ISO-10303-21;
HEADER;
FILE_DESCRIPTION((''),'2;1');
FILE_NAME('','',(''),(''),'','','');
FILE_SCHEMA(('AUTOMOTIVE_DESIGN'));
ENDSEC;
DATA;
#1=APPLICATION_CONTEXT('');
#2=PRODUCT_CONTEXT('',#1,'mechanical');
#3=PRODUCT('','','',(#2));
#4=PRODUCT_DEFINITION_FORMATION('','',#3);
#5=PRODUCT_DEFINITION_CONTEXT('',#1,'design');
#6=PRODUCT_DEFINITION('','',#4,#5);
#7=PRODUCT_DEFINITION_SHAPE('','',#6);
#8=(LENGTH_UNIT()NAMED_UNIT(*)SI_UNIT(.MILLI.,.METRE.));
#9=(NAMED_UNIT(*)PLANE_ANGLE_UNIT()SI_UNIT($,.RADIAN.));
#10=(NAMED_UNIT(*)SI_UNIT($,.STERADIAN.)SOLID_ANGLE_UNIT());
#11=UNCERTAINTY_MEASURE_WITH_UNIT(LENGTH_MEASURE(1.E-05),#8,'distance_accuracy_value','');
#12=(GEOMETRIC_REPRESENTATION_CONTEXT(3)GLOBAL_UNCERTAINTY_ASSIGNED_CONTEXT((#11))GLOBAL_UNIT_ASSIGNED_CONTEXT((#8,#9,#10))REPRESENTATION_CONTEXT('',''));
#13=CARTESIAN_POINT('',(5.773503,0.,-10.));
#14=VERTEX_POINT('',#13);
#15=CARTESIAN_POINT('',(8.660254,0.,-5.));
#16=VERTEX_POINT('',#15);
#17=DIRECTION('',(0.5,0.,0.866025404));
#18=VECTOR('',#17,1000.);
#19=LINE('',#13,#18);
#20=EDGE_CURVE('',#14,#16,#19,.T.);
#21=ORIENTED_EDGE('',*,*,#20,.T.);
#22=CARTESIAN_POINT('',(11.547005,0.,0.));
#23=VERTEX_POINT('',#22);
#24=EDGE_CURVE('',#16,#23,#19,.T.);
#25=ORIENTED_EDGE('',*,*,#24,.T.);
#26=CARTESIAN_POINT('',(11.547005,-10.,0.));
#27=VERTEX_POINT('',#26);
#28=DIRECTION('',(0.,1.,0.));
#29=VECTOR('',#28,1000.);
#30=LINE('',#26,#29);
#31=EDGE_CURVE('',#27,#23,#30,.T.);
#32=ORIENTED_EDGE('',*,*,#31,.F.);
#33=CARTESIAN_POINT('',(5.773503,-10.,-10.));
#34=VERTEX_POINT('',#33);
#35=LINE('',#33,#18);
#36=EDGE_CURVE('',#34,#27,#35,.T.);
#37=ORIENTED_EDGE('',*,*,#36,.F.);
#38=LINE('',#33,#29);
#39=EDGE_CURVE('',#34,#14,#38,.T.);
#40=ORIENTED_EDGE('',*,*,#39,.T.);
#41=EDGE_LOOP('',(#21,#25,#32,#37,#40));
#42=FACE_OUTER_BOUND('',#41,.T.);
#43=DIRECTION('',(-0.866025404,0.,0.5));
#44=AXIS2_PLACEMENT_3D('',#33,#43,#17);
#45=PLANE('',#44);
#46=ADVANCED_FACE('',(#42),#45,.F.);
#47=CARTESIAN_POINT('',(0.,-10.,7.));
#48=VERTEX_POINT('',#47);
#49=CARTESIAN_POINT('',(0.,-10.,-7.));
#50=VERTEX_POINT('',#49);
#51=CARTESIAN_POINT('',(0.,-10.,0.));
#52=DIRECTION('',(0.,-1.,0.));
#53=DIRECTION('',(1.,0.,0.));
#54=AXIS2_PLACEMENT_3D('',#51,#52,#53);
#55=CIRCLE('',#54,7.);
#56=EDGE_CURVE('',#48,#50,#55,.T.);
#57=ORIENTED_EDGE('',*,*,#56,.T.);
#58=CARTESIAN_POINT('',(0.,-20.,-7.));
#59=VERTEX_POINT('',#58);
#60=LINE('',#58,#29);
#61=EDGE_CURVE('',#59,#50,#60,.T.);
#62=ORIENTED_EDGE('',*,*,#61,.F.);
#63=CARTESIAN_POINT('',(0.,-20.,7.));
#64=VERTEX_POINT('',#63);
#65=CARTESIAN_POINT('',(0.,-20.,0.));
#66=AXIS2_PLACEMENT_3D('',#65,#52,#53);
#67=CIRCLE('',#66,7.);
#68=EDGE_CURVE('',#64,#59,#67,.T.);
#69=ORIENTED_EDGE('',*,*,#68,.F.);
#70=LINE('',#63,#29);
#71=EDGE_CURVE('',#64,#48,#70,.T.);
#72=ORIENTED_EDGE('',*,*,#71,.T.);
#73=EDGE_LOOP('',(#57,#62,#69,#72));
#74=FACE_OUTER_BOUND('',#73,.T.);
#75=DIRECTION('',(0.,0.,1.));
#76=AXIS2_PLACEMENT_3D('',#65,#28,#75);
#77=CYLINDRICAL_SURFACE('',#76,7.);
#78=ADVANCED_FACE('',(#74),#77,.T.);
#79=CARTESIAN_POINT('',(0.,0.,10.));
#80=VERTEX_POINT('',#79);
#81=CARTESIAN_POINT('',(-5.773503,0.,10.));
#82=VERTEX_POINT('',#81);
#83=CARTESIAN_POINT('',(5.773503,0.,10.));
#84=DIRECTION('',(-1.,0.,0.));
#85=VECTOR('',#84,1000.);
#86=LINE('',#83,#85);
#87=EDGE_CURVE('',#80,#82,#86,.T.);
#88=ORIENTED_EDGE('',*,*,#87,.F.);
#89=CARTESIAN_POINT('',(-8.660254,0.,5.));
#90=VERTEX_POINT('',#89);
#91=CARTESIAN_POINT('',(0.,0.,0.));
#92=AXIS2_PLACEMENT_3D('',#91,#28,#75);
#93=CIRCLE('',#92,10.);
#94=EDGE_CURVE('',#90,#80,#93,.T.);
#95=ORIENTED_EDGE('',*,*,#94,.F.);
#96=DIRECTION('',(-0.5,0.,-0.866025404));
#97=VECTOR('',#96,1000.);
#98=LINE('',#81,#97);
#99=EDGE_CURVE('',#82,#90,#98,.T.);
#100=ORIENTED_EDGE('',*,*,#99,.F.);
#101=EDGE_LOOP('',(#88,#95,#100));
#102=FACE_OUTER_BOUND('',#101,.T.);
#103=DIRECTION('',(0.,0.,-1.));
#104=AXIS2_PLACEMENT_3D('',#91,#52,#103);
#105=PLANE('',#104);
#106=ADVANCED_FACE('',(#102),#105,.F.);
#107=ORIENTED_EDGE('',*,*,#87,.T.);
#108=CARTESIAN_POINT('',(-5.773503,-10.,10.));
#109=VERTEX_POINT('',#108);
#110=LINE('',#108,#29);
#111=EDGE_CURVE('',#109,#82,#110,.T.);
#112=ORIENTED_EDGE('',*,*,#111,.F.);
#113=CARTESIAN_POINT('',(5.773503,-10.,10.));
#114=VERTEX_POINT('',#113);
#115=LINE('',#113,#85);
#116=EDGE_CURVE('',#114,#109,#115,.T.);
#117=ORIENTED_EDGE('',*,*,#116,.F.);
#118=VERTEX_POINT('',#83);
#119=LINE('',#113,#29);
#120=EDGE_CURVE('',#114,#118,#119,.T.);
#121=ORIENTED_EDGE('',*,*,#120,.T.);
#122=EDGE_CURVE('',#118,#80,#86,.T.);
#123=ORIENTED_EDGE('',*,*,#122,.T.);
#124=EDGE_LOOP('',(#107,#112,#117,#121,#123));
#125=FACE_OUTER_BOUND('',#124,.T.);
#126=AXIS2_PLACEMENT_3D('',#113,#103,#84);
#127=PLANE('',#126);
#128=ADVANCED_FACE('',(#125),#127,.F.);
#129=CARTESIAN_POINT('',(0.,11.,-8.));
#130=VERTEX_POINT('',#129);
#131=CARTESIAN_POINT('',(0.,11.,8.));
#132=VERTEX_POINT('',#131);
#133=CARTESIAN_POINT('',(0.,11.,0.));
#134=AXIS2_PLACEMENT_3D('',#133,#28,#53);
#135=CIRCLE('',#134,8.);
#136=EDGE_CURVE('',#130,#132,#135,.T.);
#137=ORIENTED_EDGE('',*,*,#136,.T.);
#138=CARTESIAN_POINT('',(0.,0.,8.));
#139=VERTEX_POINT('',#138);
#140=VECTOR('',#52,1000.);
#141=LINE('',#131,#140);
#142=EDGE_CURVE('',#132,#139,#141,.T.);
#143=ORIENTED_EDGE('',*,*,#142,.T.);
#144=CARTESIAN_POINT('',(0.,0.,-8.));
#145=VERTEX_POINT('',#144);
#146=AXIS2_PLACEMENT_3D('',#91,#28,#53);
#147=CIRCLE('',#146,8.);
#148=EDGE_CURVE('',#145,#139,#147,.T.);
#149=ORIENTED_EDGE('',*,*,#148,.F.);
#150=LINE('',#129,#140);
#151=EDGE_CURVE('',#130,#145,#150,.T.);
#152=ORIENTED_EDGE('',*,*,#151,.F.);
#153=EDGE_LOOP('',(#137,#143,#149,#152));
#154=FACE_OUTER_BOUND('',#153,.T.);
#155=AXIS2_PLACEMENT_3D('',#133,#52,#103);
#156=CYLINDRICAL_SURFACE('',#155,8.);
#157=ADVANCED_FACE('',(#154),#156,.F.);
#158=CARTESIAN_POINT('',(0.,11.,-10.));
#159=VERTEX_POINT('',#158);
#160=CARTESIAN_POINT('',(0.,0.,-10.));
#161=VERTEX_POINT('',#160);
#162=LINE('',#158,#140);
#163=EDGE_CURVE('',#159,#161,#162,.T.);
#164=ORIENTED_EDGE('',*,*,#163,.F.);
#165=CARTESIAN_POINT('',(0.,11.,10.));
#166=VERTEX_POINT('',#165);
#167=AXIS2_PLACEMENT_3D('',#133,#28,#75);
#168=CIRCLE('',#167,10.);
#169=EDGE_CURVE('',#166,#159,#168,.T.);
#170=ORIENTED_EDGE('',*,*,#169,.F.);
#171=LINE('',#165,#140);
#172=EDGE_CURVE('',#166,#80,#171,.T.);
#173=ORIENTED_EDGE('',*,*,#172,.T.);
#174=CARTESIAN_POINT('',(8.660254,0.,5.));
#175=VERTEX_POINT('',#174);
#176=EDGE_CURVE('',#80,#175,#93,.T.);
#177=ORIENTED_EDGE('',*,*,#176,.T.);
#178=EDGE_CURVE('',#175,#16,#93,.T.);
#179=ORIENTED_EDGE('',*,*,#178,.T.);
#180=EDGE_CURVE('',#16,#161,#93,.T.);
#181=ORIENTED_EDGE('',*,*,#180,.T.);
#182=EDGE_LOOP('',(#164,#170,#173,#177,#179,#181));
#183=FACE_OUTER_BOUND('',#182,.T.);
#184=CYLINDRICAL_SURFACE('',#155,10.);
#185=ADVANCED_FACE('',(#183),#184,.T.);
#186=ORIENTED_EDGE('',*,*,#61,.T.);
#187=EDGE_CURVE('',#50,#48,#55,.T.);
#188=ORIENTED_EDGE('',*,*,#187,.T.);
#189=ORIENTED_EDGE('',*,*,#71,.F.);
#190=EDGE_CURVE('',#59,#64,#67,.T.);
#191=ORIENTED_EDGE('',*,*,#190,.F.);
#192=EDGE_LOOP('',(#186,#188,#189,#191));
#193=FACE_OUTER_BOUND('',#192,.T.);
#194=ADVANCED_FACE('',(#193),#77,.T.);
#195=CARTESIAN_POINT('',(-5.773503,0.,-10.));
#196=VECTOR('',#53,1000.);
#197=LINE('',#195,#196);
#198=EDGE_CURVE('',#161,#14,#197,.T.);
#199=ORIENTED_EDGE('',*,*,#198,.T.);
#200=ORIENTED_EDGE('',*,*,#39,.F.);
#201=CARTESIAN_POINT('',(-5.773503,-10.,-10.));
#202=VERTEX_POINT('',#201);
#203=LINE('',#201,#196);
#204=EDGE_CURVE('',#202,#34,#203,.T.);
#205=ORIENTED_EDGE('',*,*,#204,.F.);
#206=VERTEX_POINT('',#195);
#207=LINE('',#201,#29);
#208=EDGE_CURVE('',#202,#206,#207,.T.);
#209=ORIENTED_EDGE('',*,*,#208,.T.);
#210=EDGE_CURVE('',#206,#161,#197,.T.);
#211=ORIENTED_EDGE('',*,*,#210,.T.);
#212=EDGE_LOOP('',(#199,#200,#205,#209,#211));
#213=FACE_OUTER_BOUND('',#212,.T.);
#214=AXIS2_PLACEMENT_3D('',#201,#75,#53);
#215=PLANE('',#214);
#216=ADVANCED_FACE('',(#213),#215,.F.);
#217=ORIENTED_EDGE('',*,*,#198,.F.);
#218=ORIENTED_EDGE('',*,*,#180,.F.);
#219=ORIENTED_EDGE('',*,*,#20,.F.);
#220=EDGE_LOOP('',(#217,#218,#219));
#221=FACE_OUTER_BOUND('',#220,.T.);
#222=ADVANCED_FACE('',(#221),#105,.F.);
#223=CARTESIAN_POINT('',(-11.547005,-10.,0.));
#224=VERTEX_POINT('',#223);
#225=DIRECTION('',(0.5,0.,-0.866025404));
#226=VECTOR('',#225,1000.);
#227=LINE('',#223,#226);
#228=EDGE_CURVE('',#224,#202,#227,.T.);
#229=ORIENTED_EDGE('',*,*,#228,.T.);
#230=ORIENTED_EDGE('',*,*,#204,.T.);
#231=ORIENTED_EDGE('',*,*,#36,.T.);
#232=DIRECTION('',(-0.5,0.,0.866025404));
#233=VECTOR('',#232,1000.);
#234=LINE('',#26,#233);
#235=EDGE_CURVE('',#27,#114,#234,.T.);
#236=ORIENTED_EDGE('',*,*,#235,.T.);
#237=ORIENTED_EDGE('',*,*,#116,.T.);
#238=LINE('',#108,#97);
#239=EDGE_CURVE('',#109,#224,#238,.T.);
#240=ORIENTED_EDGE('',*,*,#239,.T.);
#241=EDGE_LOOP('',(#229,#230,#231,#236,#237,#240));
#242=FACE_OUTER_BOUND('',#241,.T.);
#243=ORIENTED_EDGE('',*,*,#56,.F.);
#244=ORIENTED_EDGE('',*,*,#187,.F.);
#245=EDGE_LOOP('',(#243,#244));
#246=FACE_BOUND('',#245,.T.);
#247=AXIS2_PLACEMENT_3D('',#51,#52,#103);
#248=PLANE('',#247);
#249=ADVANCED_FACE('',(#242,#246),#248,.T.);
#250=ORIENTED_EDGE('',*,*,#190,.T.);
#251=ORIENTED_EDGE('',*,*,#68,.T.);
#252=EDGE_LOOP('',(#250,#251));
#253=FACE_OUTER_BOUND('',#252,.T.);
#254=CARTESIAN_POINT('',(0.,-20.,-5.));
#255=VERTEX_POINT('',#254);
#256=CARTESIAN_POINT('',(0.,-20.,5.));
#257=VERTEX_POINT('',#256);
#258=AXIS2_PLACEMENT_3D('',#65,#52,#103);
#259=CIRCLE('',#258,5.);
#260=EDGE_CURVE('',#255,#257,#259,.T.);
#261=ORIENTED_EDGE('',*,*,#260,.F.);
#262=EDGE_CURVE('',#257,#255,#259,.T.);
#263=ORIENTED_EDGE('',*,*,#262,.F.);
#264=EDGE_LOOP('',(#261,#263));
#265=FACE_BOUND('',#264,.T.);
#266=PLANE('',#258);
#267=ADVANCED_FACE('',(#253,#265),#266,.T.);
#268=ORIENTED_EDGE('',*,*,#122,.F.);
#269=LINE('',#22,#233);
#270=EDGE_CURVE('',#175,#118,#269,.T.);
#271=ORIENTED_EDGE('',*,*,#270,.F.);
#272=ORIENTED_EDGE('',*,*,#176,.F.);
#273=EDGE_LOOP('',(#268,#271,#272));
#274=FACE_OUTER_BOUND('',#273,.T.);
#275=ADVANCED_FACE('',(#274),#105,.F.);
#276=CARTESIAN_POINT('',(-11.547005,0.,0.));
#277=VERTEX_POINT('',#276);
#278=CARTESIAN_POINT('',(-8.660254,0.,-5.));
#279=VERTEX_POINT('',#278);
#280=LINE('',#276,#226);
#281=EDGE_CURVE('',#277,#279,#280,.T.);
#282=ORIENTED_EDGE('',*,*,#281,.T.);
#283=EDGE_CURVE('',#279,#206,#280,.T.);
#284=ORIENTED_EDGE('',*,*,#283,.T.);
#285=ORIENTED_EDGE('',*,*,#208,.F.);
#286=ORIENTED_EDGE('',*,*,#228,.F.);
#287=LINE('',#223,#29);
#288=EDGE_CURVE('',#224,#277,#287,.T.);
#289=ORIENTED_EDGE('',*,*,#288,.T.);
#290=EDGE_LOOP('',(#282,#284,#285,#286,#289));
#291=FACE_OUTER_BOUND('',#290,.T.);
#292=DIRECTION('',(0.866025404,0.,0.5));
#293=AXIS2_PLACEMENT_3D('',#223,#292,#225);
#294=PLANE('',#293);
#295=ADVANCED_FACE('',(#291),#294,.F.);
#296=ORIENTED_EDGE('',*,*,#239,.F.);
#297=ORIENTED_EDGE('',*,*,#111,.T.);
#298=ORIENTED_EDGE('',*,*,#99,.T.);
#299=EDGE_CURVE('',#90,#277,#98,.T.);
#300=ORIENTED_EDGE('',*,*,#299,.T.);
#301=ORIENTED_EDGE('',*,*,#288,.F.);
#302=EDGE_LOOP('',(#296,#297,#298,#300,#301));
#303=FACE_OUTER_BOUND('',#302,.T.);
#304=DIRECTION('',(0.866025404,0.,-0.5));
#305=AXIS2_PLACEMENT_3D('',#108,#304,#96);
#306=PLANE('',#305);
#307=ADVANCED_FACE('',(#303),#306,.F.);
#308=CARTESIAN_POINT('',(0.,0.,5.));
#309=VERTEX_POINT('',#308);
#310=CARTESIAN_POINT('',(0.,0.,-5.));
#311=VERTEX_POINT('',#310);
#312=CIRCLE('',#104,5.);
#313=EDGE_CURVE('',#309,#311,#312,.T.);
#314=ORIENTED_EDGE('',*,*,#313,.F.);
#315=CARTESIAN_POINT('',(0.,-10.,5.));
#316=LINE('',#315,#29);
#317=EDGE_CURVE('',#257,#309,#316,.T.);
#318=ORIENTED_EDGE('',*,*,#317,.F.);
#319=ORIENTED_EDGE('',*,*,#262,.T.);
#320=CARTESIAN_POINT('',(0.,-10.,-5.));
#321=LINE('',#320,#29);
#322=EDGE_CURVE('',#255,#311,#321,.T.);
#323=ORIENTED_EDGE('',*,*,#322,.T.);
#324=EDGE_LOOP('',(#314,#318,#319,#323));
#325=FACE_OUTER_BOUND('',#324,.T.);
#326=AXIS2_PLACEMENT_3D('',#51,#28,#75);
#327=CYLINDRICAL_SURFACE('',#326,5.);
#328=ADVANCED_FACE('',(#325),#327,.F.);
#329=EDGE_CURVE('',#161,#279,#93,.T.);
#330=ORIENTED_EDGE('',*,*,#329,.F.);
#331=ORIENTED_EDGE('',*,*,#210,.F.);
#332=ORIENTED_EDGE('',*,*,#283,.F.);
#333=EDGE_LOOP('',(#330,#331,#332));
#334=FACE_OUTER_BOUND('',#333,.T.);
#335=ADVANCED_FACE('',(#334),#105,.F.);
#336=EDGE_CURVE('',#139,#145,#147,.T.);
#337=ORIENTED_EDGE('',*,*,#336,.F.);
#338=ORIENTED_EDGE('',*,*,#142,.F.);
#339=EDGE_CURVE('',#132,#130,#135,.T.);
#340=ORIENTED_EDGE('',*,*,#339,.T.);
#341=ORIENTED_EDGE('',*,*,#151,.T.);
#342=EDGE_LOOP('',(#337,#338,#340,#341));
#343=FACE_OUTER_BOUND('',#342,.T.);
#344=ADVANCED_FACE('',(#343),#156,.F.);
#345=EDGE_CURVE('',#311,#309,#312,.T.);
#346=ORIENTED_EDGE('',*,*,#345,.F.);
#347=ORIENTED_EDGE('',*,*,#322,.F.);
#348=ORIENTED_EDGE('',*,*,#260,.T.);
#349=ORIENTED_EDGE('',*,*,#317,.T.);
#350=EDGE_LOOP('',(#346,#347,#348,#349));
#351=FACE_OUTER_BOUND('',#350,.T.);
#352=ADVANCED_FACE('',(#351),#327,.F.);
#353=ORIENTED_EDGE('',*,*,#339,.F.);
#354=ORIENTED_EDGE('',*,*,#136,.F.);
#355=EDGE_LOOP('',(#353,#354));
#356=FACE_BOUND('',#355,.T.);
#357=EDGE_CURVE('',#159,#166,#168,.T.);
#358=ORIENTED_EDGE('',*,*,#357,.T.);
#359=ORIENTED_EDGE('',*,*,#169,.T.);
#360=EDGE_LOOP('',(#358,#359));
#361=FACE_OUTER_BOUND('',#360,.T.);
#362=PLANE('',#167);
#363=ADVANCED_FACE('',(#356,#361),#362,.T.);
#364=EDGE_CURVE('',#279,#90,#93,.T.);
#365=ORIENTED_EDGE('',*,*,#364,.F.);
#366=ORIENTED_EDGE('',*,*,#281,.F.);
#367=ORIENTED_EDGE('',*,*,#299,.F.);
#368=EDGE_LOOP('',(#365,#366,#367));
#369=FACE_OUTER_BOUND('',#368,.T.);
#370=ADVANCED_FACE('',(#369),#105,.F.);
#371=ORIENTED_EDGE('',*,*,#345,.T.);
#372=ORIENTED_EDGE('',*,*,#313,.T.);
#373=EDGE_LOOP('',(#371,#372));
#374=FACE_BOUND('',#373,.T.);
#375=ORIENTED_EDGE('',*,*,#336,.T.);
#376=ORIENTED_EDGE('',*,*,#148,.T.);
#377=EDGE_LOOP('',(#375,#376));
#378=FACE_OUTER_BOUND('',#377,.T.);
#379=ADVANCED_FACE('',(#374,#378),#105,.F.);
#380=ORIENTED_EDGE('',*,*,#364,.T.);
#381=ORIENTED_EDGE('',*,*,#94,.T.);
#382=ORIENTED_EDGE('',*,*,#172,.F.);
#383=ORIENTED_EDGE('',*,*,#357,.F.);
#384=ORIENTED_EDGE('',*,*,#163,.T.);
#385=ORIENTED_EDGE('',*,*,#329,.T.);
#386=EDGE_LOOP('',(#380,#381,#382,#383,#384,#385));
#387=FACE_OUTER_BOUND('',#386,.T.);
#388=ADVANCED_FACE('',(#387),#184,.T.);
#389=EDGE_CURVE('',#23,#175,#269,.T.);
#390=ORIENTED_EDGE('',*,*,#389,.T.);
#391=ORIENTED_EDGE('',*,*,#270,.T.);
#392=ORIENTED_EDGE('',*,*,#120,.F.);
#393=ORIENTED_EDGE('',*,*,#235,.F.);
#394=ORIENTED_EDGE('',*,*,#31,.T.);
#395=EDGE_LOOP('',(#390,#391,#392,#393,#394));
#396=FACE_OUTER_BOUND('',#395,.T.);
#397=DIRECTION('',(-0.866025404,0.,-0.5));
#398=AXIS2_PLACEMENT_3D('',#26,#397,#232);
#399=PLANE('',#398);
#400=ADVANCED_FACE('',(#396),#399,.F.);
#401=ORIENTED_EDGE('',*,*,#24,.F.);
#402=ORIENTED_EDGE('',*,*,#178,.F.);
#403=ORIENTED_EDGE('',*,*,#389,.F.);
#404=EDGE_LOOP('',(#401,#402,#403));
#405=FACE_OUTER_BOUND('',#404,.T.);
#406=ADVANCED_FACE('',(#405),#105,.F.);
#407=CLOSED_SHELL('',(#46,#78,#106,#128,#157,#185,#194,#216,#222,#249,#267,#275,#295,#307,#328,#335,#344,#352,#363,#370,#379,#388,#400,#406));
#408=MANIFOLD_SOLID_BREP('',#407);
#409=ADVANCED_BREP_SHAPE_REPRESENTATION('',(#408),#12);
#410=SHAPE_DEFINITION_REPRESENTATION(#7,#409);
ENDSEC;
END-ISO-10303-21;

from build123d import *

# Parameters (mm, degrees)
SKETCH_1_R        = 10
SKETCH_1_R_2      = 8
EXTRUDE_1_DEPTH   = 11
SKETCH_2_R        = 5
EXTRUDE_1_2_DEPTH = 10
SKETCH_3_R        = 7
SKETCH_3_R_2      = 5
EXTRUDE_2_DEPTH   = 10


with BuildPart() as part:
    # 草图1 → Extrude 1 (new body)
    with BuildSketch(Plane(origin=(0, 0, 0), x_dir=(1, 0, 0), z_dir=(0, 1, 0))):
        Circle(SKETCH_1_R)
        Circle(SKETCH_1_R_2, mode=Mode.SUBTRACT)
    extrude(amount=EXTRUDE_1_DEPTH)

    # 草图2 → Extrude 1 2 (add)
    with BuildSketch(Plane.XZ):
        Polygon((11.547005384, 0), (5.773502692, 10), (-5.773502692, 10), (-11.547005384, 0), (-5.773502692, -10), (5.773502692, -10), align=None)
        with Locations(Location((0, 0, 0), (0, 0, 270))):
            Circle(SKETCH_2_R, mode=Mode.SUBTRACT)
    extrude(amount=EXTRUDE_1_2_DEPTH)

    # 草图3 → 拉伸-薄壁2 (add)
    with BuildSketch(Plane.XZ.offset(10)):
        Circle(SKETCH_3_R)
        Circle(SKETCH_3_R_2, mode=Mode.SUBTRACT)
    extrude(amount=EXTRUDE_2_DEPTH)


solid = part.part
